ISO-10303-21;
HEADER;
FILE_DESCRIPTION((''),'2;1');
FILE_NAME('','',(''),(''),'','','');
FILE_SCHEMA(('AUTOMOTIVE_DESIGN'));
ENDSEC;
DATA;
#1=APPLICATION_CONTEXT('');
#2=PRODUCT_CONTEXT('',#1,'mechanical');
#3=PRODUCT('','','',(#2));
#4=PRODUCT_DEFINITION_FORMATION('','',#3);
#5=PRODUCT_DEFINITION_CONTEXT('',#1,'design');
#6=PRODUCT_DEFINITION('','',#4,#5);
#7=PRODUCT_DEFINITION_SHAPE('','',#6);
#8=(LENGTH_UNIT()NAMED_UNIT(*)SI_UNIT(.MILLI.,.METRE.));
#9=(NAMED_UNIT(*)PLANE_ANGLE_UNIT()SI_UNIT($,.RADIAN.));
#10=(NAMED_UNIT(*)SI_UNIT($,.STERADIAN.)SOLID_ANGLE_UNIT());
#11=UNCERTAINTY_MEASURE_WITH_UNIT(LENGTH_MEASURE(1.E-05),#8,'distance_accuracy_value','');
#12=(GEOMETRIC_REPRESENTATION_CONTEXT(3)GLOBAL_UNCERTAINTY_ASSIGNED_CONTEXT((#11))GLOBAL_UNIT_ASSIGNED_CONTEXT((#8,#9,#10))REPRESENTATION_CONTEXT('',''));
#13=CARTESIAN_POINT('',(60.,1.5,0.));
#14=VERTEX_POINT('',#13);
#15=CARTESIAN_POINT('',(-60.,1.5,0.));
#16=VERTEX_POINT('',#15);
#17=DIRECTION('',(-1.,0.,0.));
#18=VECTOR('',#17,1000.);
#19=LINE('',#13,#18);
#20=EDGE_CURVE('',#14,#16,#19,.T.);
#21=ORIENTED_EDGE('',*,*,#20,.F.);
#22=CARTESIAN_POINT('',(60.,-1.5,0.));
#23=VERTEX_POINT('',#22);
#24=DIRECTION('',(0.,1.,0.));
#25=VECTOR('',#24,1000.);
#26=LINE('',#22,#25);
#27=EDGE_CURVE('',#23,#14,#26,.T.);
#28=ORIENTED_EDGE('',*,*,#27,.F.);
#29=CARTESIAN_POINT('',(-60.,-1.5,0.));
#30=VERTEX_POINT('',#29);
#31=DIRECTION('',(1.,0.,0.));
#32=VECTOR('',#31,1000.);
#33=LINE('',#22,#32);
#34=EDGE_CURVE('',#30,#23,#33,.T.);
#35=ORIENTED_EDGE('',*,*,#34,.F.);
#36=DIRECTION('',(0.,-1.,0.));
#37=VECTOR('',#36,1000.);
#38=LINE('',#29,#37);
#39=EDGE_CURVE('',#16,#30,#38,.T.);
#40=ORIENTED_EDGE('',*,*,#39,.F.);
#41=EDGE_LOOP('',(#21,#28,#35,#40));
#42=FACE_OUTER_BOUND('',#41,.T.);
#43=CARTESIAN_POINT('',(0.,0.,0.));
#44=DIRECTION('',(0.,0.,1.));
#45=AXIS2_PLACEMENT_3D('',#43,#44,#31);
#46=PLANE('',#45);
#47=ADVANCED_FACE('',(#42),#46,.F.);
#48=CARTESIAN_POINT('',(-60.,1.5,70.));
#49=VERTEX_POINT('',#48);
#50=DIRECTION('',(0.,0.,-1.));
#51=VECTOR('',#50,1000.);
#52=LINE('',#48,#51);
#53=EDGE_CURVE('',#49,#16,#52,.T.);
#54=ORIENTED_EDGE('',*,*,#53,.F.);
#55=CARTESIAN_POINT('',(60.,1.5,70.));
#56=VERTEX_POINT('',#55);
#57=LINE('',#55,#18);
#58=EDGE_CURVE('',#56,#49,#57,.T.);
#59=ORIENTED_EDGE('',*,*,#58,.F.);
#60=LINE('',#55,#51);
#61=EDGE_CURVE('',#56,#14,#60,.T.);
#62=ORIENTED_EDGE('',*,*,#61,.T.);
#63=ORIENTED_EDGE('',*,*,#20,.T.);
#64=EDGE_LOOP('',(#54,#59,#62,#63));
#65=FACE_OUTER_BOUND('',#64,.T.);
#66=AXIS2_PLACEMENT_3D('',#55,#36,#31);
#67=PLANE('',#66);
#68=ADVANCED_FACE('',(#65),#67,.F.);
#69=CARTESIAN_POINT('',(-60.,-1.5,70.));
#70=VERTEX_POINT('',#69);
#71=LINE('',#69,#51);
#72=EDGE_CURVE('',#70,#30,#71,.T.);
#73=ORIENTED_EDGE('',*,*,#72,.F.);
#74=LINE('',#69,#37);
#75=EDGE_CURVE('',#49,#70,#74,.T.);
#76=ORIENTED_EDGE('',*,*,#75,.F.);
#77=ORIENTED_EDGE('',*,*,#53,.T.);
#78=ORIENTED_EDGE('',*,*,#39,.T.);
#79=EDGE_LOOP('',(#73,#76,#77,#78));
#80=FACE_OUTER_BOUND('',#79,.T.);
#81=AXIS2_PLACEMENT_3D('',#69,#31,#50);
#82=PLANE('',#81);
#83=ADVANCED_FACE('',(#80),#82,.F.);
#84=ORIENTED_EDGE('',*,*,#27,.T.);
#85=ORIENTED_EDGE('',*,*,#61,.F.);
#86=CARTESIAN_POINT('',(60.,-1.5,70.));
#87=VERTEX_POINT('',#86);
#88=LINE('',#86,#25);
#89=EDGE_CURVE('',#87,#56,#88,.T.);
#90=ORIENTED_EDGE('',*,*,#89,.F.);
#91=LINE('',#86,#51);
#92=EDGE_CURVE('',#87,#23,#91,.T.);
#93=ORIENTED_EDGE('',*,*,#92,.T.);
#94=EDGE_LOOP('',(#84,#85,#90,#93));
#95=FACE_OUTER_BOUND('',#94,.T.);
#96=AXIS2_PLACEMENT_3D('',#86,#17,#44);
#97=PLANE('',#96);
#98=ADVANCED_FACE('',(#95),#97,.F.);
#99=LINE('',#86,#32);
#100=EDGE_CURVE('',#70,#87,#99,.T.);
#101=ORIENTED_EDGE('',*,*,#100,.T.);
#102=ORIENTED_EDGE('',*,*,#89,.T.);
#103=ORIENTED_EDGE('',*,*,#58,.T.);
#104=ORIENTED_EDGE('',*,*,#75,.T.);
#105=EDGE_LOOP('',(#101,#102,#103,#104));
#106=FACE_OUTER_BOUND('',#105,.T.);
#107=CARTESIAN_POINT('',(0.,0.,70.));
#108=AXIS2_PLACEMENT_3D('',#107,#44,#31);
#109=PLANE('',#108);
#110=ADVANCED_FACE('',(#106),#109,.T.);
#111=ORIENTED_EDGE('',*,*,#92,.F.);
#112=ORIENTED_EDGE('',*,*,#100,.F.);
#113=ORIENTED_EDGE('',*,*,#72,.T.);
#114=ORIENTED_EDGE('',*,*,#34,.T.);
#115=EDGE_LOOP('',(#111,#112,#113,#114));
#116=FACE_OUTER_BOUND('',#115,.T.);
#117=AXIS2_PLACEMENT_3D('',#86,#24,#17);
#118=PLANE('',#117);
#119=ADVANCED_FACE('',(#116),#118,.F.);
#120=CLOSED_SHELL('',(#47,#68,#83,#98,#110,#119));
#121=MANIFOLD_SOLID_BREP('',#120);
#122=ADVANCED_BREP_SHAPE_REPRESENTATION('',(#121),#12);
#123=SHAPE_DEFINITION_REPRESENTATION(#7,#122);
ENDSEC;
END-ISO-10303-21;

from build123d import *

# Parameters (mm, degrees)
SKETCH_1_W      = 120
SKETCH_1_H      = 3
EXTRUDE_1_DEPTH = 70


with BuildPart() as part:
    # 草图1 → 凸台-拉伸1 (new body)
    with BuildSketch(Plane.XY):
        Rectangle(SKETCH_1_W, SKETCH_1_H)
    extrude(amount=EXTRUDE_1_DEPTH)


solid = part.part
